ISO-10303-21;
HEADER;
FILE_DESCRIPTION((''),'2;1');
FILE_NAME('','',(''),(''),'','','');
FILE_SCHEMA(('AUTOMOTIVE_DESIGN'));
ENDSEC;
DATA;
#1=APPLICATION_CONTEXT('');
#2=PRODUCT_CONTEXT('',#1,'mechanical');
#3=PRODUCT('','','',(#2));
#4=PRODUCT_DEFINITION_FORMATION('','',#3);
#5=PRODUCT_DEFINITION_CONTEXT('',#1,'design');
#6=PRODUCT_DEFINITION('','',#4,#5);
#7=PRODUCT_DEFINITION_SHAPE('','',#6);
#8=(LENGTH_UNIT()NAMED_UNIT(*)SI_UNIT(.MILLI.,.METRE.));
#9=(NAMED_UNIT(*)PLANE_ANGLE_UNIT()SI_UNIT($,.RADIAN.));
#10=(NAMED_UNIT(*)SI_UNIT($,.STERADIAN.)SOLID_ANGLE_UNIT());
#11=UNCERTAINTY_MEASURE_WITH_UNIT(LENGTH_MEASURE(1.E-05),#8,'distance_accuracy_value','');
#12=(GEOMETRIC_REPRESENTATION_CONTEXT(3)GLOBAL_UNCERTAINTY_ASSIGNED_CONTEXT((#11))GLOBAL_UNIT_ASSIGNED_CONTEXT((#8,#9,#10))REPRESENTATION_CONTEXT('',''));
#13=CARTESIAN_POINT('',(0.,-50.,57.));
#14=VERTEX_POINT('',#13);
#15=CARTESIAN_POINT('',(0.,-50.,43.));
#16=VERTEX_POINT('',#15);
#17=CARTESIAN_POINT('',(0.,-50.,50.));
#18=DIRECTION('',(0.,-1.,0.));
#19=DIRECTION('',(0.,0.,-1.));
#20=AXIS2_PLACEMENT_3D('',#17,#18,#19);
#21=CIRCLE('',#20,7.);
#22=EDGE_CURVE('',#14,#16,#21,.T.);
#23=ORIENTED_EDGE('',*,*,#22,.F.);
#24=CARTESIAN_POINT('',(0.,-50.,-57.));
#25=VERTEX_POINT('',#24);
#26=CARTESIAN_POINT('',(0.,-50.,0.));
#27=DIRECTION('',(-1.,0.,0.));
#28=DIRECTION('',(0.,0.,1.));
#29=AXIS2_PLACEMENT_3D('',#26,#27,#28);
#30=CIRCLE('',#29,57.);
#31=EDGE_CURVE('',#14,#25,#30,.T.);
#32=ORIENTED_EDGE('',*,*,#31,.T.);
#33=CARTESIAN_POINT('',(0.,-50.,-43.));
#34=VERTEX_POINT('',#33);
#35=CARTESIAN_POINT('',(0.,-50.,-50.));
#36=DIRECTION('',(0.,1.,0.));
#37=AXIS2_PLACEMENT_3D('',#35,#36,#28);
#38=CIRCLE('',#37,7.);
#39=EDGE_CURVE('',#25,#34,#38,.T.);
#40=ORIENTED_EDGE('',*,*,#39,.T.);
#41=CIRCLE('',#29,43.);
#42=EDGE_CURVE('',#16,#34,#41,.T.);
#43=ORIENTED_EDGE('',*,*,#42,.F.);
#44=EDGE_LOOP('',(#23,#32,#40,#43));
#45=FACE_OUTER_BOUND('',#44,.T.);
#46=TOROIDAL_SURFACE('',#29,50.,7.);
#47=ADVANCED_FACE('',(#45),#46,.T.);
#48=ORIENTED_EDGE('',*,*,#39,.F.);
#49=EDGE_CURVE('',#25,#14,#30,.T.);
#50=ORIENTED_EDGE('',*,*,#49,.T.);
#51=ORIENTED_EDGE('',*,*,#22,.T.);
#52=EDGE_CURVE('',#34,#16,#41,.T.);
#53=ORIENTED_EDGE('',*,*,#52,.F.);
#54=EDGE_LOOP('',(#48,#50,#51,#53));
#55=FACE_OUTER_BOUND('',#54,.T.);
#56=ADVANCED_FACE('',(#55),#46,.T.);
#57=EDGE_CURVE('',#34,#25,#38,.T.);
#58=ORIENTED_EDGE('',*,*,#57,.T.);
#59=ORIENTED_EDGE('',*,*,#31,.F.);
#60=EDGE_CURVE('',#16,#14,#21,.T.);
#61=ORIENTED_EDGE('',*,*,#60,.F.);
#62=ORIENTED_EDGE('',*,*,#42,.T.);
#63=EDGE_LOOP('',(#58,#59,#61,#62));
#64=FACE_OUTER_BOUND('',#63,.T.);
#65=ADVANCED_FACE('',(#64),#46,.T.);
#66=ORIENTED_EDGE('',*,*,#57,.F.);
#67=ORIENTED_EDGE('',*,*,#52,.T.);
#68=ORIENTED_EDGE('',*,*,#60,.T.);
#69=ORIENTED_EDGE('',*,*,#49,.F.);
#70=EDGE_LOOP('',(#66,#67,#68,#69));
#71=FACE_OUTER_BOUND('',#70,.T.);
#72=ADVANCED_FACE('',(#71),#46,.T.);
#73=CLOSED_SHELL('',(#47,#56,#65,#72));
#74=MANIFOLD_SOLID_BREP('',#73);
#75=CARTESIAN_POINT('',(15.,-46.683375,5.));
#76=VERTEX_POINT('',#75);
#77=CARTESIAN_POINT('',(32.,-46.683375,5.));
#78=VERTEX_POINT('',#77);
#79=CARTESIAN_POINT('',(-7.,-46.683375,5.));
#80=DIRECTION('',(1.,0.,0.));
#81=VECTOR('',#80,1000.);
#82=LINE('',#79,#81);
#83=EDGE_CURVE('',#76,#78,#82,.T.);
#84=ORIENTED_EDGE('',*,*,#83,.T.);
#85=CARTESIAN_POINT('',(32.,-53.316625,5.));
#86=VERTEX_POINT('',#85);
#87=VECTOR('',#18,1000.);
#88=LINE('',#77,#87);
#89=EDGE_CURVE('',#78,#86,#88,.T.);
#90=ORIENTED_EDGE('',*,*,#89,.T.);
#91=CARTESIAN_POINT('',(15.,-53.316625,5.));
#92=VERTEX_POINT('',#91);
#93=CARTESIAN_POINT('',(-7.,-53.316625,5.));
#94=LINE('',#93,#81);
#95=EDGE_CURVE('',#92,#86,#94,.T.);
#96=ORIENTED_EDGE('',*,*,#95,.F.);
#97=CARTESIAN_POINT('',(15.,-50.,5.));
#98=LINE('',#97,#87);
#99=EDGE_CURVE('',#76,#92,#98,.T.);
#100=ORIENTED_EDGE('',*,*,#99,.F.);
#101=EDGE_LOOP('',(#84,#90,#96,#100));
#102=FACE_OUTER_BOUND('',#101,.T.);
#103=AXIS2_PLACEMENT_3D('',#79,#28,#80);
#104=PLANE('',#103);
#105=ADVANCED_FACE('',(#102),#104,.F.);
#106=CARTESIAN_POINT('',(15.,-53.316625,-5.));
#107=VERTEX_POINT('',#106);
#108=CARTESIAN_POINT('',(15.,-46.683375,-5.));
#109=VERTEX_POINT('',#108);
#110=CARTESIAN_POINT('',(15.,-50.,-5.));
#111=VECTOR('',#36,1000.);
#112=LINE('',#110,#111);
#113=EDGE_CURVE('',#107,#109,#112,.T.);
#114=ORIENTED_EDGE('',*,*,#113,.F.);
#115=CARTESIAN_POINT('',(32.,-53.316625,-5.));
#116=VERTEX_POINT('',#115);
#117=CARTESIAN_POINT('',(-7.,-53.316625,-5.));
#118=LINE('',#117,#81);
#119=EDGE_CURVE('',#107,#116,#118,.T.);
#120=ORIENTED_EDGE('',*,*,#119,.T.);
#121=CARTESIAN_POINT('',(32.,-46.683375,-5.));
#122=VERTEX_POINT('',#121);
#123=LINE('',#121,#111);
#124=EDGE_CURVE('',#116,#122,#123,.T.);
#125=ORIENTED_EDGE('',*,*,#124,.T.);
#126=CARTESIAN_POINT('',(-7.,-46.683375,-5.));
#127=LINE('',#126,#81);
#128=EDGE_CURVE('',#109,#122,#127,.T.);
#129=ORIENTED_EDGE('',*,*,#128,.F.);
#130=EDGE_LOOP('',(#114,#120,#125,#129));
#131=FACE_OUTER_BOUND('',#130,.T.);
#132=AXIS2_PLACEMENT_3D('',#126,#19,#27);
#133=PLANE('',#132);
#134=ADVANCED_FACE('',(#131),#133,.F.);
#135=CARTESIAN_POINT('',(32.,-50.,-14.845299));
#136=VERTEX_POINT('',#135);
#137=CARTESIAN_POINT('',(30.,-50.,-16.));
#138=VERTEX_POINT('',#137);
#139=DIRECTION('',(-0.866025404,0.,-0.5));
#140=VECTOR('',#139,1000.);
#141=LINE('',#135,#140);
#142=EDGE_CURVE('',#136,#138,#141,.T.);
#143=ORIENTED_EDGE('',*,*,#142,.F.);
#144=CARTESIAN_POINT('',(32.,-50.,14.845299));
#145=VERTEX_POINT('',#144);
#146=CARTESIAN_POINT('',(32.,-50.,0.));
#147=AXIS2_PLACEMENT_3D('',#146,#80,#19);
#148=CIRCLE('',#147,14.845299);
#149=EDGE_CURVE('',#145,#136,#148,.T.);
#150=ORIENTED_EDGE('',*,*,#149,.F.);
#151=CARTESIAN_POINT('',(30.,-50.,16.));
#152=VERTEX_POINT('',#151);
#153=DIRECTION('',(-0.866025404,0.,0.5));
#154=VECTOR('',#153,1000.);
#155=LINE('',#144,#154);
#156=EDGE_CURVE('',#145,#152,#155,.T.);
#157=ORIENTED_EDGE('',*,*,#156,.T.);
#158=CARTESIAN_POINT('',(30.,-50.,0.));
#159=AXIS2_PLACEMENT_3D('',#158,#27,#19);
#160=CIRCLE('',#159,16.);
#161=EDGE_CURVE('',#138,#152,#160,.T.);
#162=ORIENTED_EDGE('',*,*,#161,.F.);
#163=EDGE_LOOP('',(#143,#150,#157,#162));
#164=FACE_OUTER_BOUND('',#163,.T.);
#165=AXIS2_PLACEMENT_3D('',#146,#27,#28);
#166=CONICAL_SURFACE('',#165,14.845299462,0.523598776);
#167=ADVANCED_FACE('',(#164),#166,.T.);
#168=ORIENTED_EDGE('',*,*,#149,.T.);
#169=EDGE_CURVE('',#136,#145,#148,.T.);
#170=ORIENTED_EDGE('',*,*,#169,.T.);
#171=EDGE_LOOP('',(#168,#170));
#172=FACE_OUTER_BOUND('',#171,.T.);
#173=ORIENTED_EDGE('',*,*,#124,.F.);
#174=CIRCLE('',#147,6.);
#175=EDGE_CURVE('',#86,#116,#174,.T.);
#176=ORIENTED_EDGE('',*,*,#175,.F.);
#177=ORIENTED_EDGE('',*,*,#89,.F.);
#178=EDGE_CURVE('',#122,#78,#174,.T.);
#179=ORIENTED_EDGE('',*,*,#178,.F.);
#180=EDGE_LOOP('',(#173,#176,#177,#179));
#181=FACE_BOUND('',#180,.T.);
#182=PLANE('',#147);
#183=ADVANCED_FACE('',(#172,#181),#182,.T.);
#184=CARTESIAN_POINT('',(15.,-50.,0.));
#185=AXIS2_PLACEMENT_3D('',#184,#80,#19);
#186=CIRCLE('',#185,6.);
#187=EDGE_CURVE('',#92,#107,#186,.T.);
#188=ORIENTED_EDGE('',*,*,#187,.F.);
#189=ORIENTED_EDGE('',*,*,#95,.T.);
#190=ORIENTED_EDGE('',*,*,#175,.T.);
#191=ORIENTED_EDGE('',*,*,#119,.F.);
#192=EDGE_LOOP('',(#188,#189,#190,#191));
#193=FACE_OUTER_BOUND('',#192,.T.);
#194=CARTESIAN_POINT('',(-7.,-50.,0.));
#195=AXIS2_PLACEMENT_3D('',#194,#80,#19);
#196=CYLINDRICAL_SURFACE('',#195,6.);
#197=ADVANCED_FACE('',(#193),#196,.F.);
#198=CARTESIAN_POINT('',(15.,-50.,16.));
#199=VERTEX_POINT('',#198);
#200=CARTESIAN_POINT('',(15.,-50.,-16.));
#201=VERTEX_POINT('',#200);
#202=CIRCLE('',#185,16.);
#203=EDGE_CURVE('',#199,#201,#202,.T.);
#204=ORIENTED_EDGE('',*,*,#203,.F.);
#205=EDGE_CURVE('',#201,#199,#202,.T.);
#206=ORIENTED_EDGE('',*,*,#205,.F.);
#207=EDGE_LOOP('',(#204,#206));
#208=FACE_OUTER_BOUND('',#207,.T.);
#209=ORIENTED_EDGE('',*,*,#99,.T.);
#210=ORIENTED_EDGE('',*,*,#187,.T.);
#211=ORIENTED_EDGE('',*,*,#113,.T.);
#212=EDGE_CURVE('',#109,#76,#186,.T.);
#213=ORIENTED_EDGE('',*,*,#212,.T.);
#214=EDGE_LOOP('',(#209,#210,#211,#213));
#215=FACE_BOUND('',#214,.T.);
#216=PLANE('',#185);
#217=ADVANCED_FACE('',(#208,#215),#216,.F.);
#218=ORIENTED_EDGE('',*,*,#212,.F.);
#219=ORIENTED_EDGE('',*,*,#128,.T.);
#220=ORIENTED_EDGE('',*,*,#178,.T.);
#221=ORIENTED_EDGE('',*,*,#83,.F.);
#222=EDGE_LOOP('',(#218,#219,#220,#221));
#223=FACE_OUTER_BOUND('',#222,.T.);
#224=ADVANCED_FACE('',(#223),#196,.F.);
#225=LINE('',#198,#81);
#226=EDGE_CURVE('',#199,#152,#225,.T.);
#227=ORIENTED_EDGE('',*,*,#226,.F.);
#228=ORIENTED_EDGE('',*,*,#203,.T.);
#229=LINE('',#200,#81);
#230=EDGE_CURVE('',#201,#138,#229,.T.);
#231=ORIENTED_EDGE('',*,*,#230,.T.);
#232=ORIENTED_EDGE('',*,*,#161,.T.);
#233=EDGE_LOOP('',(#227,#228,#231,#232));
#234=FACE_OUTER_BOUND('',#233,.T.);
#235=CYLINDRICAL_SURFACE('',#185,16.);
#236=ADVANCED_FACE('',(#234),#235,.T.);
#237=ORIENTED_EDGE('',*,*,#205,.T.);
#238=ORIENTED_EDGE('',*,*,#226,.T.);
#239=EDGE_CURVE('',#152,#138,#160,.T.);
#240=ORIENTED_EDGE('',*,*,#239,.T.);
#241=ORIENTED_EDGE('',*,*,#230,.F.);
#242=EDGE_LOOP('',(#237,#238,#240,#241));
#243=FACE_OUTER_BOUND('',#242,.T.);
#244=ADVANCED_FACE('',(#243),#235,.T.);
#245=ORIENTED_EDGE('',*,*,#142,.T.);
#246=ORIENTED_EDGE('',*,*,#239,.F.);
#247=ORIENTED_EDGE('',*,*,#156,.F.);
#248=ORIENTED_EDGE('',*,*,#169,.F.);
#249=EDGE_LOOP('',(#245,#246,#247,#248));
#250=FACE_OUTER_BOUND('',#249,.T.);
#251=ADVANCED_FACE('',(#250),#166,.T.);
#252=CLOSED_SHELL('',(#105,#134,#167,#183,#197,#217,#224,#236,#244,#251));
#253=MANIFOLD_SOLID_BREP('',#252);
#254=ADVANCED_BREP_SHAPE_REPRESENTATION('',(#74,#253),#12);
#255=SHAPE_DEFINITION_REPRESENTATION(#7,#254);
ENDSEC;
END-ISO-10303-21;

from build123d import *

# Parameters (mm, degrees)
SKETCH1_R           = 7
SKETCH3_R           = 16
BOSS_EXTRUDE1_DEPTH = 17
CHAMFER1_SIZE       = 2
CHAMFER1_SIZE2      = 1.154700538
CUT_EXTRUDE1_DEPTH  = 128.35383795


with BuildPart() as part:
    # Sweep1: sweep along a path in Sketch2
    with BuildLine(Plane(origin=(0, 0, 0), x_dir=(0, 0, -1), z_dir=(1, 0, 0))) as sweep1_path:
        CenterArc((0, -50), 50, 0, 360)
    # Sketch1 → Sweep1 (sweep)
    with BuildSketch(Plane.XY):
        Circle(SKETCH1_R)
    sweep(path=sweep1_path.line)


with BuildPart() as body_2:
    # Sketch3 → Boss-Extrude1 (new body)
    with BuildSketch(Plane(origin=(32, 0, 0), x_dir=(0, 0, -1), z_dir=(1, 0, 0))):
        with Locations((0, -50)):
            Circle(SKETCH3_R)
    extrude(amount=-BOSS_EXTRUDE1_DEPTH)

    # Chamfer1
    chamfer1_edges = [body_2.edges().sort_by_distance(p)[0] for p in [
        (32, -50, 16),
    ]]
    chamfer1_side = [body_2.faces().sort_by_distance(p)[0] for p in [
        (23.5, -50, 16),
    ]]
    chamfer(chamfer1_edges, length=CHAMFER1_SIZE, length2=CHAMFER1_SIZE2, reference=chamfer1_side[0])

    # Sketch6 → Cut-Extrude1 (cut, through all)
    with BuildSketch(Plane(origin=(32, 0, 0), x_dir=(0, 0, -1), z_dir=(1, 0, 0))):
        with BuildLine():
            Line((-5, -46.68337521), (-5, -53.31662479))
            ThreePointArc((-5, -53.31662479), (0, -56), (5, -53.31662479))
            Line((5, -53.31662479), (5, -46.68337521))
            ThreePointArc((5, -46.68337521), (0, -44), (-5, -46.68337521))
        make_face()
    extrude(amount=-CUT_EXTRUDE1_DEPTH, mode=Mode.SUBTRACT)


solid = Compound([part.part, body_2.part])
